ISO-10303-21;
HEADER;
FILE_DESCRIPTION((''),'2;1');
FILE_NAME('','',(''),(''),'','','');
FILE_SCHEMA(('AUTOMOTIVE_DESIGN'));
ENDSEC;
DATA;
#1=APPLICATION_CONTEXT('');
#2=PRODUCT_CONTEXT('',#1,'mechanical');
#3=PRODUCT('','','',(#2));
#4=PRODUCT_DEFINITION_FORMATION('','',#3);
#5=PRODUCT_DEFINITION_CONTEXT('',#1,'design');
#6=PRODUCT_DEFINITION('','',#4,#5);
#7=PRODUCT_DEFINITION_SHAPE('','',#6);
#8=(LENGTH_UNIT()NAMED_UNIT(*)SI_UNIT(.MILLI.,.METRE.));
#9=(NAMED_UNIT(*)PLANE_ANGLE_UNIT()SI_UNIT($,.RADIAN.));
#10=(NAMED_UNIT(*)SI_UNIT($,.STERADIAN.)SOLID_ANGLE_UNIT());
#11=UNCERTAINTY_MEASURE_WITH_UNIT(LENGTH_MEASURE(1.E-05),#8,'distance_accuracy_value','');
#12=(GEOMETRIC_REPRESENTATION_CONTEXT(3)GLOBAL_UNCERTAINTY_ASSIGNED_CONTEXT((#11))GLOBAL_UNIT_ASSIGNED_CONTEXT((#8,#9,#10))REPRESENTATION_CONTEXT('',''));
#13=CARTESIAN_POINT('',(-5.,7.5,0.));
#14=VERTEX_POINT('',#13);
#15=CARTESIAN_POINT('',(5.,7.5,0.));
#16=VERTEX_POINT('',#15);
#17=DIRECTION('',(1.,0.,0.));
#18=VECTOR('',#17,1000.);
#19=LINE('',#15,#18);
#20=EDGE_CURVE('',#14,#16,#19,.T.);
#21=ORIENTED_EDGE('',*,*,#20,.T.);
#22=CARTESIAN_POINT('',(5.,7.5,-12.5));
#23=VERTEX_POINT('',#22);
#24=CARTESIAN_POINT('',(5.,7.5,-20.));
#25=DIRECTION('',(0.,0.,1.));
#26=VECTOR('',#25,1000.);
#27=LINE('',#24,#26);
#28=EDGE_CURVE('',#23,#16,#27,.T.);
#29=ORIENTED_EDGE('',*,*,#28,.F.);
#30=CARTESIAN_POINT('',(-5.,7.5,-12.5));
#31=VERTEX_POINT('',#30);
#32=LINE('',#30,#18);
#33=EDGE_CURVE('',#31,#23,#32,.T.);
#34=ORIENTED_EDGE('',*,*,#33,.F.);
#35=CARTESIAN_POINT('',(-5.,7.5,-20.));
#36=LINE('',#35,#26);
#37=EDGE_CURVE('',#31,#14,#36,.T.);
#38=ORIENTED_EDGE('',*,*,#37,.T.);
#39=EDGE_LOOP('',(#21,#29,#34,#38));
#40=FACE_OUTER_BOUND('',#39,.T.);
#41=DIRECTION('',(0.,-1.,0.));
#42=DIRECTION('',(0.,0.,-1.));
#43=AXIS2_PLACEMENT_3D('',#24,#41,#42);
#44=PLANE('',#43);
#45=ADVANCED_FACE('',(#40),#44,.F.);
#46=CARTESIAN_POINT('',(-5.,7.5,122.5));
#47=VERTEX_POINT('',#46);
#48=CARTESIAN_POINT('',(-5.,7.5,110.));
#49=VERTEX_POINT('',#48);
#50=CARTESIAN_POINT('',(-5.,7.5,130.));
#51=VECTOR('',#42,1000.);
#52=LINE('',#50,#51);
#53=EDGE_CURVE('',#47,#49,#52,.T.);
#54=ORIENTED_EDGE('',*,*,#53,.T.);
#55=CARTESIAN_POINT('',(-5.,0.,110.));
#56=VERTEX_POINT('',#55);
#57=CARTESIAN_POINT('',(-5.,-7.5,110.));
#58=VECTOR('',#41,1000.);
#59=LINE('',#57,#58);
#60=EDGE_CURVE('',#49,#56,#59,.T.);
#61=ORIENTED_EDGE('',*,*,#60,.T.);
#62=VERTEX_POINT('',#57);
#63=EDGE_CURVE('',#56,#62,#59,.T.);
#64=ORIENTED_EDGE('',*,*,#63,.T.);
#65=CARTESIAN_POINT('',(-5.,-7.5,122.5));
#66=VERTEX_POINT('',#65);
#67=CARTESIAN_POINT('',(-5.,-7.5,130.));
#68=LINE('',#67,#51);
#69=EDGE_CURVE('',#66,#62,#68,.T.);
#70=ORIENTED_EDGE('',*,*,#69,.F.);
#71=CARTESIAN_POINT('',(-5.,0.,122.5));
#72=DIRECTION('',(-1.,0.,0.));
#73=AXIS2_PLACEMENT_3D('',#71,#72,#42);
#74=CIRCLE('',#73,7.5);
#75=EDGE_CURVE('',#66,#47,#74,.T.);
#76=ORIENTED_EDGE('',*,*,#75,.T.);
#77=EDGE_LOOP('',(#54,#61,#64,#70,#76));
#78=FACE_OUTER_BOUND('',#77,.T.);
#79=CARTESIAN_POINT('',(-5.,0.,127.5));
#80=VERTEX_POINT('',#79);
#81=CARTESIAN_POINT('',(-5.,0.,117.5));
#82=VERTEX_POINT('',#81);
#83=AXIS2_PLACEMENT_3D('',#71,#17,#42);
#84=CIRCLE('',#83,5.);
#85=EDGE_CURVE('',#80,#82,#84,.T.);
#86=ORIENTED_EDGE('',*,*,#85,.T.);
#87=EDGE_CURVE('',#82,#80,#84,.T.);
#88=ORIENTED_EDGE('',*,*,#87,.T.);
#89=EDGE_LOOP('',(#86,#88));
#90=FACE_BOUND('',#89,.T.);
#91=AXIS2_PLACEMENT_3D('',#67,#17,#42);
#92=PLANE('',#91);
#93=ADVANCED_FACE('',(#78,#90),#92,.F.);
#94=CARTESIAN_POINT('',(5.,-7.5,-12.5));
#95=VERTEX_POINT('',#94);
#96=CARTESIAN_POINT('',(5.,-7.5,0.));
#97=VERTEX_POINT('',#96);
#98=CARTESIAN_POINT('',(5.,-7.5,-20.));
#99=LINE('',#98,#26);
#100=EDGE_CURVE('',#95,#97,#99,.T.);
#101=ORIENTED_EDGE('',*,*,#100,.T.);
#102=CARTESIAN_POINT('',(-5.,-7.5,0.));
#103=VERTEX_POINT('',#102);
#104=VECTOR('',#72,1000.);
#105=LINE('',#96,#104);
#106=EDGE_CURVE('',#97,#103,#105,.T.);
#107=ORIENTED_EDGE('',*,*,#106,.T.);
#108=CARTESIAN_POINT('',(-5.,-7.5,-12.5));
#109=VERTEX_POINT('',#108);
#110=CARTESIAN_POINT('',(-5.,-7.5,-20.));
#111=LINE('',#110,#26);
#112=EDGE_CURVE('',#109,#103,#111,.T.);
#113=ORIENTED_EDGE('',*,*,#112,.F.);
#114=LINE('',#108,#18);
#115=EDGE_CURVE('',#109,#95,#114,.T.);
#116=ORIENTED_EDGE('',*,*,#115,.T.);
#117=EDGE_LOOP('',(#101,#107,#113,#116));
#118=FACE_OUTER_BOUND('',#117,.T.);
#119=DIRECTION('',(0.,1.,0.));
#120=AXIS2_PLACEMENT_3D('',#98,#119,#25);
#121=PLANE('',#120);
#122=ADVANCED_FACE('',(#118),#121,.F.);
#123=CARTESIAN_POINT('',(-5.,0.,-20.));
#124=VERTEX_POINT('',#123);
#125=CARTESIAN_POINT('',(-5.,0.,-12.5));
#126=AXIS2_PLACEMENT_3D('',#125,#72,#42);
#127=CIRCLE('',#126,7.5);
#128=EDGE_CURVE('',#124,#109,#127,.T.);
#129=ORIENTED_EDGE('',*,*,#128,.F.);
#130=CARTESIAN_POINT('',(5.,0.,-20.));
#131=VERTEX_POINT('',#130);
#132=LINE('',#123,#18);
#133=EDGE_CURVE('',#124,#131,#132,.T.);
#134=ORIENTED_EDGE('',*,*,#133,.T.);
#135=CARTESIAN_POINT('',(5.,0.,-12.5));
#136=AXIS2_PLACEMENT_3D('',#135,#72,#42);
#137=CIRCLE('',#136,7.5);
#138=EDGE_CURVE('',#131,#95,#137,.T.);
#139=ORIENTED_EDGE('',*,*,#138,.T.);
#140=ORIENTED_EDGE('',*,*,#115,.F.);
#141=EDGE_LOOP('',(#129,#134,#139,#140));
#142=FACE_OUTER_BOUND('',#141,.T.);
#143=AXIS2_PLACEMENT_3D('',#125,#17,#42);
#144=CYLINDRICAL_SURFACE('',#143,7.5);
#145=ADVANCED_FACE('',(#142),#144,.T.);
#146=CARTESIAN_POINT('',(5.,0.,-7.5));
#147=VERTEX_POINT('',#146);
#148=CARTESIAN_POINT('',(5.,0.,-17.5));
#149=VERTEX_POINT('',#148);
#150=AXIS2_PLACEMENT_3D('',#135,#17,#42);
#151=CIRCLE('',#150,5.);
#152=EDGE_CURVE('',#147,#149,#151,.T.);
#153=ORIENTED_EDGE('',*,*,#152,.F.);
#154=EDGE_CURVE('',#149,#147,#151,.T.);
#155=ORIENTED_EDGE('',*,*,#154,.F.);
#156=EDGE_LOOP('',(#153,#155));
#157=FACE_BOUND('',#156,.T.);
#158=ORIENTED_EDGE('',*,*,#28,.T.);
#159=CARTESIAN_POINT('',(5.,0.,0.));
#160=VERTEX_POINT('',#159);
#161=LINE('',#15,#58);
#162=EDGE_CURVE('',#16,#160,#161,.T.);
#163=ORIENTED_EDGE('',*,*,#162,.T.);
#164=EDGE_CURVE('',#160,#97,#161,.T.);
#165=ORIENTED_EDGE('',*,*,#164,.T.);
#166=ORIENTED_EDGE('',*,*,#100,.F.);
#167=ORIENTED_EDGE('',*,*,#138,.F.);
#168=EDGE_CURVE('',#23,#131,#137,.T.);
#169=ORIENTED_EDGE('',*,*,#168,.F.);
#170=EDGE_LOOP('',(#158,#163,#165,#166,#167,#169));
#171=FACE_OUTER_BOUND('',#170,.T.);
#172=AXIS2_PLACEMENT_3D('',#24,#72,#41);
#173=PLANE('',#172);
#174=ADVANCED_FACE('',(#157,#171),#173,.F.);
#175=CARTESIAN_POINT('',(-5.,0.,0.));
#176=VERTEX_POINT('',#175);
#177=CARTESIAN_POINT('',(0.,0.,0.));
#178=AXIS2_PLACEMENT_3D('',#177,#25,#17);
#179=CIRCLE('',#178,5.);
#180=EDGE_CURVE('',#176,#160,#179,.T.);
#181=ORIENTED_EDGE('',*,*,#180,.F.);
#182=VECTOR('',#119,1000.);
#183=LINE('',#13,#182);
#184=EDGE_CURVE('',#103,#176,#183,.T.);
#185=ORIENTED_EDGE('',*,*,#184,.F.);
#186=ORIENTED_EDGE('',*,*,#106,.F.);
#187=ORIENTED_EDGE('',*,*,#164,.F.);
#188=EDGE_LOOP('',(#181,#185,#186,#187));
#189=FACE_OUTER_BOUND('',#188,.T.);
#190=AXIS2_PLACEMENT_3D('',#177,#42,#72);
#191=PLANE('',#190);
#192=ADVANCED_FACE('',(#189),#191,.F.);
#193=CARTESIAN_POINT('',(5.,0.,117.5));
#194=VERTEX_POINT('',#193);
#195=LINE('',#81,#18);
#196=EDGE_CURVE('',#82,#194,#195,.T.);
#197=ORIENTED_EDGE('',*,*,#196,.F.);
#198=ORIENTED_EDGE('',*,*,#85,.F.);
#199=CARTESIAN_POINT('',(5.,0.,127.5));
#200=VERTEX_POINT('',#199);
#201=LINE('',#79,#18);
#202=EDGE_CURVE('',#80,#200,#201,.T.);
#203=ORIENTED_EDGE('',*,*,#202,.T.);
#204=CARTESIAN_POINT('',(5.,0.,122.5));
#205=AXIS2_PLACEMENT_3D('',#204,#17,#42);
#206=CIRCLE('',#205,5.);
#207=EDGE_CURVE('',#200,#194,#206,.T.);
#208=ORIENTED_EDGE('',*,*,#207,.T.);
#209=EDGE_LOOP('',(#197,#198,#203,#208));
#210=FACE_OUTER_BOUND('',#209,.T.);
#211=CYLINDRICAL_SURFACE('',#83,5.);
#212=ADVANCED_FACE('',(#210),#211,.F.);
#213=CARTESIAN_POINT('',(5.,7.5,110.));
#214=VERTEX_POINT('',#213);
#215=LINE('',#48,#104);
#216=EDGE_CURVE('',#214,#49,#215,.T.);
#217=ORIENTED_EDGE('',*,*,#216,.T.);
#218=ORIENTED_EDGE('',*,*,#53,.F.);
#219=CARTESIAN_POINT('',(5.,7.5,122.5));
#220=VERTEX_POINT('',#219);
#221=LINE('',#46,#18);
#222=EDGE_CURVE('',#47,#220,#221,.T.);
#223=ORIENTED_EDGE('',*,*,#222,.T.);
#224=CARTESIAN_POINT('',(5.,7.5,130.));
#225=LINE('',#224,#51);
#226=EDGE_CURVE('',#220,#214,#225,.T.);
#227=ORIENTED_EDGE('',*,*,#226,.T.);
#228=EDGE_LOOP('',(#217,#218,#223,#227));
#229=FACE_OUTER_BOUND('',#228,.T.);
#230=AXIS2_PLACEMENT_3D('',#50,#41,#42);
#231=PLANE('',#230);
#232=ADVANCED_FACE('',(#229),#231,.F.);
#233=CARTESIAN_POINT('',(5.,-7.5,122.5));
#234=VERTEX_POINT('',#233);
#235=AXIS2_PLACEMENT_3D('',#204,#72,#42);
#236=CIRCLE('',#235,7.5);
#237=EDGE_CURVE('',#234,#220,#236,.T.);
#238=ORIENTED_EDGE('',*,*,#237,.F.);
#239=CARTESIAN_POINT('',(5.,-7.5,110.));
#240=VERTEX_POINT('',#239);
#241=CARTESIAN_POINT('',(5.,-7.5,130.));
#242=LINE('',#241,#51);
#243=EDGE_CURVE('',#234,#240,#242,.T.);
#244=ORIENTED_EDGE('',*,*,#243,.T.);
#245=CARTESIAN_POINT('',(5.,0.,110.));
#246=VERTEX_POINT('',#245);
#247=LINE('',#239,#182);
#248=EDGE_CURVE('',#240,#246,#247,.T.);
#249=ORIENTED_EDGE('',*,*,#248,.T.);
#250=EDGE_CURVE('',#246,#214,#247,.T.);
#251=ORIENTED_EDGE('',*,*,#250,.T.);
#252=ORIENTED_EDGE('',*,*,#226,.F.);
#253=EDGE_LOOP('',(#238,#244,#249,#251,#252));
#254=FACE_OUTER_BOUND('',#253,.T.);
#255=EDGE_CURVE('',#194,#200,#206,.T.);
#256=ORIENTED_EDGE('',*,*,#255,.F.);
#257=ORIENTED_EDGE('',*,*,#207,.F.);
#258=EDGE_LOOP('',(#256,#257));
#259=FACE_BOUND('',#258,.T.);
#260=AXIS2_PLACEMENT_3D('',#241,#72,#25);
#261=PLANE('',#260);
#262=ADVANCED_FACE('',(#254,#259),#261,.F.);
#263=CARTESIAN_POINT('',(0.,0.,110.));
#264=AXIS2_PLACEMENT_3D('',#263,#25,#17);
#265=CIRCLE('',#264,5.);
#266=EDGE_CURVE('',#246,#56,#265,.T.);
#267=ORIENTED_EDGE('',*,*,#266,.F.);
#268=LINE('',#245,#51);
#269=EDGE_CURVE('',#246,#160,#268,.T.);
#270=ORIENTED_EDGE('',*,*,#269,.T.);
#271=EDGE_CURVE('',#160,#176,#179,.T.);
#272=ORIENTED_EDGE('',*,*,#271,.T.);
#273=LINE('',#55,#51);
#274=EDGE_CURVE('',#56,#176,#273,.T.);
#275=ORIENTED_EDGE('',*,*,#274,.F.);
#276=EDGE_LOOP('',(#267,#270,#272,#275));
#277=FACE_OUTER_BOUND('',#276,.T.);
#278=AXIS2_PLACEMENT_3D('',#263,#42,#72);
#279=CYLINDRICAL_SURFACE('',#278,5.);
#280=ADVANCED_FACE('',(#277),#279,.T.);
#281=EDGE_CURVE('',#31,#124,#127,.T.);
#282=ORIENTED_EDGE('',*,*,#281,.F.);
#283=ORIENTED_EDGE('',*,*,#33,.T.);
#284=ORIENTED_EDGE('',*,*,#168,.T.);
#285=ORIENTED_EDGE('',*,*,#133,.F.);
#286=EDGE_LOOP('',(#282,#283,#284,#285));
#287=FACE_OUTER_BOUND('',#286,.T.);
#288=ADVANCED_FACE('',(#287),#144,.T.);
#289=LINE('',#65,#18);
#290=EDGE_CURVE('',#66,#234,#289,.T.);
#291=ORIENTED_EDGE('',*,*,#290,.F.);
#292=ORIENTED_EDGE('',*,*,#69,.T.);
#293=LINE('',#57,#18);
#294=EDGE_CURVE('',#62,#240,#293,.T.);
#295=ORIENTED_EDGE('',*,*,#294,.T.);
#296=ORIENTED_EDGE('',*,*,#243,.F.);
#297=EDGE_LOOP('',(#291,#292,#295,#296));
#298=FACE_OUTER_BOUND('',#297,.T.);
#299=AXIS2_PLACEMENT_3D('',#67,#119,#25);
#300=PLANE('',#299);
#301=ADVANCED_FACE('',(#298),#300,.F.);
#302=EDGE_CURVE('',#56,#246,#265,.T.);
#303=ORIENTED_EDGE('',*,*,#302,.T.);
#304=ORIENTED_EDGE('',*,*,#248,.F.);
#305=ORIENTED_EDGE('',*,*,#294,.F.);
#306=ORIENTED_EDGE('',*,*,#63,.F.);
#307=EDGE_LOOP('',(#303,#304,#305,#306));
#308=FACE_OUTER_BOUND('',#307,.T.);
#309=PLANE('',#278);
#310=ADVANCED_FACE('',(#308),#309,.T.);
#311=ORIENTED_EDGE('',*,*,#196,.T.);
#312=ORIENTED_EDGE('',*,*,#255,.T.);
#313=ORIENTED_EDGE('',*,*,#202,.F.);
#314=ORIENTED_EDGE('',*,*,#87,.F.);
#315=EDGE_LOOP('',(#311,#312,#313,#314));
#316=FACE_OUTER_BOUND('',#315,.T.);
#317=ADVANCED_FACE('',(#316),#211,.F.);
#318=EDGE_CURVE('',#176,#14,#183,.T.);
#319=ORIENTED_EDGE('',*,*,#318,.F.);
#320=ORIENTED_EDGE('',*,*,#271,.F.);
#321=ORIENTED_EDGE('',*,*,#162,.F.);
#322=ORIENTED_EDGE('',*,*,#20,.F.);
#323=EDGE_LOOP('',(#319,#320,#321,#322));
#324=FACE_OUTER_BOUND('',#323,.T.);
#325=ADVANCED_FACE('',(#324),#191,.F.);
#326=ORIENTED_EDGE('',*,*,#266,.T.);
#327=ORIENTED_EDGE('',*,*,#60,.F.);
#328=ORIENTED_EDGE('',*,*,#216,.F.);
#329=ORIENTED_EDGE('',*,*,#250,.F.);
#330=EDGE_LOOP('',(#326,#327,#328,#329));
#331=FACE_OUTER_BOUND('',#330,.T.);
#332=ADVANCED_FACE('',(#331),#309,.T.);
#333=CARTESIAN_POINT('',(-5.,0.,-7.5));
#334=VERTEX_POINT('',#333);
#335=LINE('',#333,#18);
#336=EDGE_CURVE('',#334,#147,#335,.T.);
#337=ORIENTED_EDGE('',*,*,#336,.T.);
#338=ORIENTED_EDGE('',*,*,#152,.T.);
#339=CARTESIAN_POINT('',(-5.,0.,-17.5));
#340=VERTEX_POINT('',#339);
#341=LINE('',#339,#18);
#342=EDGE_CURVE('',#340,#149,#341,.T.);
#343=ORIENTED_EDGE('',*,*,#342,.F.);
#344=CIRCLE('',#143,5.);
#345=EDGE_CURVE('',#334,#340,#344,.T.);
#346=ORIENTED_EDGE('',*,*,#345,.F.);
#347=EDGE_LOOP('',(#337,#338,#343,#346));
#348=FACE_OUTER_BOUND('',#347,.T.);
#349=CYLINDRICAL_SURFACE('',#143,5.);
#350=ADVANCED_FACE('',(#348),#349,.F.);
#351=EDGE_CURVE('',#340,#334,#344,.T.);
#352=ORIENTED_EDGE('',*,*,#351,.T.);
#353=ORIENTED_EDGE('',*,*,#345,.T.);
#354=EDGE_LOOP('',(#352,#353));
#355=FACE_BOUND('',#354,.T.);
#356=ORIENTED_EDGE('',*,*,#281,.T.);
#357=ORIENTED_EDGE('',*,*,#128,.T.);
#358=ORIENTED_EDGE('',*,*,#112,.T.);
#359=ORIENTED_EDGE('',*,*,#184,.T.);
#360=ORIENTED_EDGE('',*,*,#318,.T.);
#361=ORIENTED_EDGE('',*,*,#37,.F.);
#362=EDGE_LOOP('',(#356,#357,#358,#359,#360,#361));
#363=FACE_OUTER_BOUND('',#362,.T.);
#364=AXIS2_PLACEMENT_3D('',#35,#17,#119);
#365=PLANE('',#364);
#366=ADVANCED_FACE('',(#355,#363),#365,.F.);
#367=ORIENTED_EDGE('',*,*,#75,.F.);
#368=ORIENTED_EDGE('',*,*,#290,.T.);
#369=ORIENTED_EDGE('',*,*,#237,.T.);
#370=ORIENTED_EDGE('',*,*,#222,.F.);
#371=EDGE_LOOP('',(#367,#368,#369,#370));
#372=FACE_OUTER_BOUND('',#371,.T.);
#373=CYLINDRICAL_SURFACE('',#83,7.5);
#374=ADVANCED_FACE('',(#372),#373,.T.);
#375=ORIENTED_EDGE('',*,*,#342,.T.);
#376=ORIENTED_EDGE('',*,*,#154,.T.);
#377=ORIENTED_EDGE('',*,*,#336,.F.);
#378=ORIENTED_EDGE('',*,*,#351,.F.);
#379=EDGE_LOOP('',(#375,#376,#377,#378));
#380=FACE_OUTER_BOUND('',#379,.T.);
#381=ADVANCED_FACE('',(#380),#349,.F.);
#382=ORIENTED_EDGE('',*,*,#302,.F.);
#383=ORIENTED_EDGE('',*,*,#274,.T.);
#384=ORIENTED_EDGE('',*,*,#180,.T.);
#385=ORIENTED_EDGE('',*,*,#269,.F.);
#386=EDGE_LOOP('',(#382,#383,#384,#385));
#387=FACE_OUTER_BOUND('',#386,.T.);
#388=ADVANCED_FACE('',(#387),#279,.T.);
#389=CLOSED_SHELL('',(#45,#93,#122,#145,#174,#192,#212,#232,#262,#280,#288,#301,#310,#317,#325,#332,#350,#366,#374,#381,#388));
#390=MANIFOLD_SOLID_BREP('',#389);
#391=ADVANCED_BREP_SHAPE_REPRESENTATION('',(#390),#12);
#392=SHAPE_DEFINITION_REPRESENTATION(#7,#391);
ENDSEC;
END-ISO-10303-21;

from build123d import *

# Parameters (mm, degrees)
SKETCH1_R           = 5
BOSS_EXTRUDE1_DEPTH = 110
SKETCH2_W           = 10
SKETCH2_H           = 15
BOSS_EXTRUDE2_DEPTH = 20
SKETCH3_W           = 10
SKETCH3_H           = 15
BOSS_EXTRUDE3_DEPTH = 20
SKETCH4_R           = 5
CUT_EXTRUDE1_DEPTH  = 131.599578866


with BuildPart() as part:
    # Sketch1 → Boss-Extrude1 (new body)
    with BuildSketch(Plane.XY):
        Circle(SKETCH1_R)
    extrude(amount=BOSS_EXTRUDE1_DEPTH)

    # Sketch2 → Boss-Extrude2 (add)
    with BuildSketch(Plane(origin=(0, 0, 0), x_dir=(-1, 0, 0), z_dir=(0, 0, -1))):
        Rectangle(SKETCH2_W, SKETCH2_H)
    extrude(amount=BOSS_EXTRUDE2_DEPTH)

    # Sketch3 → Boss-Extrude3 (add)
    with BuildSketch(Plane.XY.offset(110)):
        Rectangle(SKETCH3_W, SKETCH3_H)
    extrude(amount=BOSS_EXTRUDE3_DEPTH)

    # Sketch4 → Cut-Extrude1 (cut, through all)
    with BuildSketch(Plane(origin=(5, 0, 0), x_dir=(0, 0, -1), z_dir=(1, 0, 0))):
        with Locations((12.5, 0)):
            Circle(SKETCH4_R)
        with Locations((-122.5, 0)):
            Circle(SKETCH4_R)
        with BuildLine():
            Line((12.5, -7.5), (27.957175819, -19.344646022))
            Line((27.957175819, -19.344646022), (25.412525065, 11.111642689))
            Line((25.412525065, 11.111642689), (12.5, 7.5))
            ThreePointArc((12.5, 7.5), (20, 0), (12.5, -7.5))
        make_face()
        with BuildLine():
            Line((-122.5, 7.5), (-386.499272389, 23.053021062))
            Line((-386.499272389, 23.053021062), (-390.004854727, -19.344646022))
            Line((-390.004854727, -19.344646022), (-122.5, -7.5))
            ThreePointArc((-122.5, -7.5), (-130, 0), (-122.5, 7.5))
        make_face()
    extrude(amount=-CUT_EXTRUDE1_DEPTH, mode=Mode.SUBTRACT)


solid = part.part
